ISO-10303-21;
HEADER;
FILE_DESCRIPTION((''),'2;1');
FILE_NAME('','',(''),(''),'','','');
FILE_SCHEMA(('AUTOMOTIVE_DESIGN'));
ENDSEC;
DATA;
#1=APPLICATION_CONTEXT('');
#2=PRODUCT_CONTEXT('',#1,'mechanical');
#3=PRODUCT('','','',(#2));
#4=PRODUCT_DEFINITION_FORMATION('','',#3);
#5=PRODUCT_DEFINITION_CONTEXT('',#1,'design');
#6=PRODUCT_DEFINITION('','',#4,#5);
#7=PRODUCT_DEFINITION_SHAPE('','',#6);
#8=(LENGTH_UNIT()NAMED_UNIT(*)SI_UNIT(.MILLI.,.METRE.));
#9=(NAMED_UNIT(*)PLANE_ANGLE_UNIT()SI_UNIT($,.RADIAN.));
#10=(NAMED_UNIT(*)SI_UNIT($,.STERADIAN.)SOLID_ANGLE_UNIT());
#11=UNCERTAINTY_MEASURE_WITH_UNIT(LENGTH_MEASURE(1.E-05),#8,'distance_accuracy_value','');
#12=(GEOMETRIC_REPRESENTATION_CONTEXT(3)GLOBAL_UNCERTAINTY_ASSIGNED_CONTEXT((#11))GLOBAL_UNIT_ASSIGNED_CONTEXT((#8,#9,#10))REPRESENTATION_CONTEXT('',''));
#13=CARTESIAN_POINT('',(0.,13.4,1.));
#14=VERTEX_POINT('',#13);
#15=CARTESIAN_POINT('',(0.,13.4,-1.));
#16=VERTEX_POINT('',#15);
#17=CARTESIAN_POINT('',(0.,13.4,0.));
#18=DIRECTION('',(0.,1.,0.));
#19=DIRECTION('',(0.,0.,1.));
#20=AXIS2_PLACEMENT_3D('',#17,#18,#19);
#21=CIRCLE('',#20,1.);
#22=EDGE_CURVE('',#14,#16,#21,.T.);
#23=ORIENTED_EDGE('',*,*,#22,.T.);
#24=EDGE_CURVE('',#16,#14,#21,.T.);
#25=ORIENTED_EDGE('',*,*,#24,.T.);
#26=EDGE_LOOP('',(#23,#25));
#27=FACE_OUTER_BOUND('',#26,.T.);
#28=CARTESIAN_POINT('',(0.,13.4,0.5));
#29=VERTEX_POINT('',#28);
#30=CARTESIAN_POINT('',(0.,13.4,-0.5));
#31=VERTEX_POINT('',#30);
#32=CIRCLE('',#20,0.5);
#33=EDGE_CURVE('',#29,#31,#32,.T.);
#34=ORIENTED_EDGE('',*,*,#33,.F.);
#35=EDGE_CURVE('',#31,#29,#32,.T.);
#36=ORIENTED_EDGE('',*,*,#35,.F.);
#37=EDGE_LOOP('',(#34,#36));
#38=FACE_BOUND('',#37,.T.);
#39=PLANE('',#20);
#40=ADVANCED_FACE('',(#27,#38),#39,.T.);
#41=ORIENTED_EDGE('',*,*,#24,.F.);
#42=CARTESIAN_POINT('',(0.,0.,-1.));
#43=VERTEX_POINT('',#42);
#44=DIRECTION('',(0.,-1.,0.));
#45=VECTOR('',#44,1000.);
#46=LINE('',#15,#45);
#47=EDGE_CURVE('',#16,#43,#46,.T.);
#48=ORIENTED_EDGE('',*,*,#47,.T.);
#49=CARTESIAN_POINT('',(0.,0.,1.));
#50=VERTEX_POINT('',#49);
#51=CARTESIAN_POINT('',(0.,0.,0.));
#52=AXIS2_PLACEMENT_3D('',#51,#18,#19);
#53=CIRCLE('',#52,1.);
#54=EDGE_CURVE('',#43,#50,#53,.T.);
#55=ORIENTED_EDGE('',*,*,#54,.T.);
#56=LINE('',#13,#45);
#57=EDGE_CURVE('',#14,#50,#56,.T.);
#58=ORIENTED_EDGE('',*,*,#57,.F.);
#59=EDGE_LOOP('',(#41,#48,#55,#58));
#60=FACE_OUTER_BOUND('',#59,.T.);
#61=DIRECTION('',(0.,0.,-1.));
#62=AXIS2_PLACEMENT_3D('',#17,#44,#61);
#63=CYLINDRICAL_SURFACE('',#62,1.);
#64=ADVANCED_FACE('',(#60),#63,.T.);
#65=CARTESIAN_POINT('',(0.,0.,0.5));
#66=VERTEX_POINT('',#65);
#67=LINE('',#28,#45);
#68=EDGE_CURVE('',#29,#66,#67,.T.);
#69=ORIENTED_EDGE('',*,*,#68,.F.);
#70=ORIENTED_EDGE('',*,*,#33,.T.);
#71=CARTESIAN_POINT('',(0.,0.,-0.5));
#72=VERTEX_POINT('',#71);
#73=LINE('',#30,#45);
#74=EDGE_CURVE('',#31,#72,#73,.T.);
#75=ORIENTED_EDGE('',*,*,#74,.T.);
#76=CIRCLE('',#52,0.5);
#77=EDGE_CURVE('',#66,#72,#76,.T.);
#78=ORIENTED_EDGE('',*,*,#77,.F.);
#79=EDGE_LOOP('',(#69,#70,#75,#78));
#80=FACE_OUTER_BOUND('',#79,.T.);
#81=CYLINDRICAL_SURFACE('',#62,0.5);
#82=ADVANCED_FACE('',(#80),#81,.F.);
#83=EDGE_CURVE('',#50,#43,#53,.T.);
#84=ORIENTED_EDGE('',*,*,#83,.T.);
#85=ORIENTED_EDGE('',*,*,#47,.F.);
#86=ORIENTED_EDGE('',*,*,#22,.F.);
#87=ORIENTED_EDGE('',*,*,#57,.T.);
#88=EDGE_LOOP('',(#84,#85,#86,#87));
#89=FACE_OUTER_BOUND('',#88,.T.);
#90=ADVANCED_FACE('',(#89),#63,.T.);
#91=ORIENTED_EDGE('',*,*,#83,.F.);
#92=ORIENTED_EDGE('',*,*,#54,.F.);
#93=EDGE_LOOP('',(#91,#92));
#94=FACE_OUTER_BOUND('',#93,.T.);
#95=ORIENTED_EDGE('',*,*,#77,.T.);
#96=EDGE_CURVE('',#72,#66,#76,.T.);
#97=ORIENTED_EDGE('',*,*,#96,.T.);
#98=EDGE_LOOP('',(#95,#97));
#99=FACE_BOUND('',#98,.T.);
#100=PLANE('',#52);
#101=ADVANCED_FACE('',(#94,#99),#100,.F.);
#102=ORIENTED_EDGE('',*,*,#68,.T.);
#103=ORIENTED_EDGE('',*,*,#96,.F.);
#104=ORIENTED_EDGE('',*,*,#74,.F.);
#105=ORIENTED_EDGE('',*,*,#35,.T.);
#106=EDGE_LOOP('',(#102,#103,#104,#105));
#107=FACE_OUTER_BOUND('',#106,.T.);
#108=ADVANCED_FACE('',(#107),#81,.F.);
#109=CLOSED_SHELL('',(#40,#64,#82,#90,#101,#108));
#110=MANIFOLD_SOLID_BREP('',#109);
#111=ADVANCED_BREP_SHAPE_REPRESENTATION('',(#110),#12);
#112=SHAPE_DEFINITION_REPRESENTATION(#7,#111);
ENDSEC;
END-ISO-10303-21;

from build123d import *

# Parameters (mm, degrees)
SKETCH1_R           = 1
SKETCH1_R_2         = 0.5
BOSS_EXTRUDE1_DEPTH = 13.4


with BuildPart() as part:
    # Sketch1 → Boss-Extrude1 (new body)
    with BuildSketch(Plane(origin=(0, 0, 0), x_dir=(1, 0, 0), z_dir=(0, 1, 0))):
        with Locations(Location((0, 0, 0), (0, 0, 270))):
            Circle(SKETCH1_R)
        with Locations(Location((0, 0, 0), (0, 0, 270))):
            Circle(SKETCH1_R_2, mode=Mode.SUBTRACT)
    extrude(amount=BOSS_EXTRUDE1_DEPTH)


solid = part.part
